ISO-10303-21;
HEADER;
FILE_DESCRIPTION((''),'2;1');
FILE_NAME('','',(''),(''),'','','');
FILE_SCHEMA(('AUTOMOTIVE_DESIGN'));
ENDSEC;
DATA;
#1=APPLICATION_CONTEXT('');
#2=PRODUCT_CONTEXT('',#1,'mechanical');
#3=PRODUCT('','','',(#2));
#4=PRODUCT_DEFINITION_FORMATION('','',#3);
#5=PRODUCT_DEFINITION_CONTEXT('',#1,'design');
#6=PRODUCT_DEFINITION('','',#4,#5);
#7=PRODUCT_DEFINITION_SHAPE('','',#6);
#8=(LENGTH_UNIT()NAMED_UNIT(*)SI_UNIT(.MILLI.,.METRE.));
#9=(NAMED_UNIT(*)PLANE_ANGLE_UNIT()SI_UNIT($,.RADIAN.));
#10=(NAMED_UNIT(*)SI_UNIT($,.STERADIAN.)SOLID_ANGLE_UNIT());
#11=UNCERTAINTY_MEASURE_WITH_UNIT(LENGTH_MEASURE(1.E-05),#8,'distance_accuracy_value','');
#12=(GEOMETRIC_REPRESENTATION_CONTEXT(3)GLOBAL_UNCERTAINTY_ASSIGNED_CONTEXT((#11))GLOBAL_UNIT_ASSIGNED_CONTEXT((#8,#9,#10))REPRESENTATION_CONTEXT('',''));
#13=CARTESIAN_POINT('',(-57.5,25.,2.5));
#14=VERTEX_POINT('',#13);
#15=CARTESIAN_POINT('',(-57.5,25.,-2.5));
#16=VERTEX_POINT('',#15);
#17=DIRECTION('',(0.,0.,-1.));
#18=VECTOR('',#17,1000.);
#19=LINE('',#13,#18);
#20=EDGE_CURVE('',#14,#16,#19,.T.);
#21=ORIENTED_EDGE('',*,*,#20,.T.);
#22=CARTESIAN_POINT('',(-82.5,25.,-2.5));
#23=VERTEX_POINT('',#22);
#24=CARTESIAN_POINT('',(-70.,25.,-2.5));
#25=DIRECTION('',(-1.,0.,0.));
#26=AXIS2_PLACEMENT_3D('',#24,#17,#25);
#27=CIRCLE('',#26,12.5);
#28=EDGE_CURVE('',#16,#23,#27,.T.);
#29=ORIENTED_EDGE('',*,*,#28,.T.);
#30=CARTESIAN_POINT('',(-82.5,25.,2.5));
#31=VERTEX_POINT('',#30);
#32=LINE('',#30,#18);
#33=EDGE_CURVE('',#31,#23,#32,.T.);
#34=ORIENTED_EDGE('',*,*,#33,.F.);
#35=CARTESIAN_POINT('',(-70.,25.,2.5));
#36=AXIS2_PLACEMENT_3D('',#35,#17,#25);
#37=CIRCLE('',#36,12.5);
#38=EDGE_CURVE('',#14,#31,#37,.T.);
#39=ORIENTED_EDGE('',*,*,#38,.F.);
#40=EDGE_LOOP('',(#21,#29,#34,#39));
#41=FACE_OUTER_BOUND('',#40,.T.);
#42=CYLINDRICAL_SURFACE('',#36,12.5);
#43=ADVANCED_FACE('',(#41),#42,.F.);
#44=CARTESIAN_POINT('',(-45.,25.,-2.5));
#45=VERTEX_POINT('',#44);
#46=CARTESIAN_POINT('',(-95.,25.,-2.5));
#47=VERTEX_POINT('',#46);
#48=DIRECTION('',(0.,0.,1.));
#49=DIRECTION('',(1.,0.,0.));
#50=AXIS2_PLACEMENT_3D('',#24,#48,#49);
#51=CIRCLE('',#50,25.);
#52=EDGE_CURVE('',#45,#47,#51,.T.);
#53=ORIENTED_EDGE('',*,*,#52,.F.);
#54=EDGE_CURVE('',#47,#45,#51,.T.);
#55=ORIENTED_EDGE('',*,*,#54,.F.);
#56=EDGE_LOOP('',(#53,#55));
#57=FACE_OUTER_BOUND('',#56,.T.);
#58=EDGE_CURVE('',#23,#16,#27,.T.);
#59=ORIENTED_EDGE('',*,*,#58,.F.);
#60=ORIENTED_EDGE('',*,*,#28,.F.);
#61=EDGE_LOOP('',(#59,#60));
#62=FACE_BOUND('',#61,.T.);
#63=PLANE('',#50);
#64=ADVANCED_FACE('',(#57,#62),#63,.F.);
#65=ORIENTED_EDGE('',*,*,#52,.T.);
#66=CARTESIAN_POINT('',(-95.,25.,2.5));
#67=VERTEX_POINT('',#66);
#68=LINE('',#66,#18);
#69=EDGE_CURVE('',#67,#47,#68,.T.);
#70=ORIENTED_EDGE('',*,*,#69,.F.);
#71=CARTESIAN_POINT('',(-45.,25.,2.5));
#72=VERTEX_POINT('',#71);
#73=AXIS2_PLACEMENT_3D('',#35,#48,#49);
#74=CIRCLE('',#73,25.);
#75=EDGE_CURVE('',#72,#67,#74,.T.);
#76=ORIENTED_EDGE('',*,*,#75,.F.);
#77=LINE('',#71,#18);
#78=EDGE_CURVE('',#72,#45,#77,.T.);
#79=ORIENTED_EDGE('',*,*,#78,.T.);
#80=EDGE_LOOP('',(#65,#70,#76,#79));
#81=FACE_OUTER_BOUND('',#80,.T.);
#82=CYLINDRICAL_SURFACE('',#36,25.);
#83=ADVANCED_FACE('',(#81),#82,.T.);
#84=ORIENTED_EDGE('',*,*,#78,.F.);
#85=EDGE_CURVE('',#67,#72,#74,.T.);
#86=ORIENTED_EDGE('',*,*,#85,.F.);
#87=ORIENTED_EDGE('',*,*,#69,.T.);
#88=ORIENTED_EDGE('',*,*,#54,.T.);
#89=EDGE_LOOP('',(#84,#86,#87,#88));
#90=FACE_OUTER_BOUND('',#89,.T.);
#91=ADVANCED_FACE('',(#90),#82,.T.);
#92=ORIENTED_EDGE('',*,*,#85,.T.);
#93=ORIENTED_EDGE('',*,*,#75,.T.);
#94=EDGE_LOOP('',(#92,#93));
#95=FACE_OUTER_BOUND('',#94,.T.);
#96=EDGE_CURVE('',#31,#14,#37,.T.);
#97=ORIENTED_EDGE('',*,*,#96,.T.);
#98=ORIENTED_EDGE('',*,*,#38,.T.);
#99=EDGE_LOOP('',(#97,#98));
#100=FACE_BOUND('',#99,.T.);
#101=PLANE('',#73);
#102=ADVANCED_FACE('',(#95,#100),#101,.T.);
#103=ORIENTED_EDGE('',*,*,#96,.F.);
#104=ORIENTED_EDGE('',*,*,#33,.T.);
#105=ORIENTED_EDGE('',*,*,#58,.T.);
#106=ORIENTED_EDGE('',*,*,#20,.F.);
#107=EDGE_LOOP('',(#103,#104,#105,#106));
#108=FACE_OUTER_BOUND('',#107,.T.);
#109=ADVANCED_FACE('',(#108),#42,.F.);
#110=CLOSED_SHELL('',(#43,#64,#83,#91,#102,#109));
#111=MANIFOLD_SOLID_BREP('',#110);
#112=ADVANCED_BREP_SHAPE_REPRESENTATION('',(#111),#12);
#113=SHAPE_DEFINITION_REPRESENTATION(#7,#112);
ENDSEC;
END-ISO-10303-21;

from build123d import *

# Parameters (mm, degrees)
SKETCH2_R           = 25
BOSS_EXTRUDE1_DEPTH = 2.5
SKETCH3_R           = 12.5
CUT_EXTRUDE1_DEPTH  = 108.470926301


with BuildPart() as part:
    # Sketch2 → Boss-Extrude1 (new, symmetric)
    with BuildSketch(Plane.XY):
        with Locations((-70, 25)):
            Circle(SKETCH2_R)
    extrude(amount=BOSS_EXTRUDE1_DEPTH, both=True)

    # Sketch3 → Cut-Extrude1 (cut, through all)
    with BuildSketch(Plane(origin=(0, 0, -2.5), x_dir=(-1, 0, 0), z_dir=(0, 0, -1))):
        with Locations((70, 25)):
            Circle(SKETCH3_R)
    extrude(amount=-CUT_EXTRUDE1_DEPTH, mode=Mode.SUBTRACT)


solid = part.part
